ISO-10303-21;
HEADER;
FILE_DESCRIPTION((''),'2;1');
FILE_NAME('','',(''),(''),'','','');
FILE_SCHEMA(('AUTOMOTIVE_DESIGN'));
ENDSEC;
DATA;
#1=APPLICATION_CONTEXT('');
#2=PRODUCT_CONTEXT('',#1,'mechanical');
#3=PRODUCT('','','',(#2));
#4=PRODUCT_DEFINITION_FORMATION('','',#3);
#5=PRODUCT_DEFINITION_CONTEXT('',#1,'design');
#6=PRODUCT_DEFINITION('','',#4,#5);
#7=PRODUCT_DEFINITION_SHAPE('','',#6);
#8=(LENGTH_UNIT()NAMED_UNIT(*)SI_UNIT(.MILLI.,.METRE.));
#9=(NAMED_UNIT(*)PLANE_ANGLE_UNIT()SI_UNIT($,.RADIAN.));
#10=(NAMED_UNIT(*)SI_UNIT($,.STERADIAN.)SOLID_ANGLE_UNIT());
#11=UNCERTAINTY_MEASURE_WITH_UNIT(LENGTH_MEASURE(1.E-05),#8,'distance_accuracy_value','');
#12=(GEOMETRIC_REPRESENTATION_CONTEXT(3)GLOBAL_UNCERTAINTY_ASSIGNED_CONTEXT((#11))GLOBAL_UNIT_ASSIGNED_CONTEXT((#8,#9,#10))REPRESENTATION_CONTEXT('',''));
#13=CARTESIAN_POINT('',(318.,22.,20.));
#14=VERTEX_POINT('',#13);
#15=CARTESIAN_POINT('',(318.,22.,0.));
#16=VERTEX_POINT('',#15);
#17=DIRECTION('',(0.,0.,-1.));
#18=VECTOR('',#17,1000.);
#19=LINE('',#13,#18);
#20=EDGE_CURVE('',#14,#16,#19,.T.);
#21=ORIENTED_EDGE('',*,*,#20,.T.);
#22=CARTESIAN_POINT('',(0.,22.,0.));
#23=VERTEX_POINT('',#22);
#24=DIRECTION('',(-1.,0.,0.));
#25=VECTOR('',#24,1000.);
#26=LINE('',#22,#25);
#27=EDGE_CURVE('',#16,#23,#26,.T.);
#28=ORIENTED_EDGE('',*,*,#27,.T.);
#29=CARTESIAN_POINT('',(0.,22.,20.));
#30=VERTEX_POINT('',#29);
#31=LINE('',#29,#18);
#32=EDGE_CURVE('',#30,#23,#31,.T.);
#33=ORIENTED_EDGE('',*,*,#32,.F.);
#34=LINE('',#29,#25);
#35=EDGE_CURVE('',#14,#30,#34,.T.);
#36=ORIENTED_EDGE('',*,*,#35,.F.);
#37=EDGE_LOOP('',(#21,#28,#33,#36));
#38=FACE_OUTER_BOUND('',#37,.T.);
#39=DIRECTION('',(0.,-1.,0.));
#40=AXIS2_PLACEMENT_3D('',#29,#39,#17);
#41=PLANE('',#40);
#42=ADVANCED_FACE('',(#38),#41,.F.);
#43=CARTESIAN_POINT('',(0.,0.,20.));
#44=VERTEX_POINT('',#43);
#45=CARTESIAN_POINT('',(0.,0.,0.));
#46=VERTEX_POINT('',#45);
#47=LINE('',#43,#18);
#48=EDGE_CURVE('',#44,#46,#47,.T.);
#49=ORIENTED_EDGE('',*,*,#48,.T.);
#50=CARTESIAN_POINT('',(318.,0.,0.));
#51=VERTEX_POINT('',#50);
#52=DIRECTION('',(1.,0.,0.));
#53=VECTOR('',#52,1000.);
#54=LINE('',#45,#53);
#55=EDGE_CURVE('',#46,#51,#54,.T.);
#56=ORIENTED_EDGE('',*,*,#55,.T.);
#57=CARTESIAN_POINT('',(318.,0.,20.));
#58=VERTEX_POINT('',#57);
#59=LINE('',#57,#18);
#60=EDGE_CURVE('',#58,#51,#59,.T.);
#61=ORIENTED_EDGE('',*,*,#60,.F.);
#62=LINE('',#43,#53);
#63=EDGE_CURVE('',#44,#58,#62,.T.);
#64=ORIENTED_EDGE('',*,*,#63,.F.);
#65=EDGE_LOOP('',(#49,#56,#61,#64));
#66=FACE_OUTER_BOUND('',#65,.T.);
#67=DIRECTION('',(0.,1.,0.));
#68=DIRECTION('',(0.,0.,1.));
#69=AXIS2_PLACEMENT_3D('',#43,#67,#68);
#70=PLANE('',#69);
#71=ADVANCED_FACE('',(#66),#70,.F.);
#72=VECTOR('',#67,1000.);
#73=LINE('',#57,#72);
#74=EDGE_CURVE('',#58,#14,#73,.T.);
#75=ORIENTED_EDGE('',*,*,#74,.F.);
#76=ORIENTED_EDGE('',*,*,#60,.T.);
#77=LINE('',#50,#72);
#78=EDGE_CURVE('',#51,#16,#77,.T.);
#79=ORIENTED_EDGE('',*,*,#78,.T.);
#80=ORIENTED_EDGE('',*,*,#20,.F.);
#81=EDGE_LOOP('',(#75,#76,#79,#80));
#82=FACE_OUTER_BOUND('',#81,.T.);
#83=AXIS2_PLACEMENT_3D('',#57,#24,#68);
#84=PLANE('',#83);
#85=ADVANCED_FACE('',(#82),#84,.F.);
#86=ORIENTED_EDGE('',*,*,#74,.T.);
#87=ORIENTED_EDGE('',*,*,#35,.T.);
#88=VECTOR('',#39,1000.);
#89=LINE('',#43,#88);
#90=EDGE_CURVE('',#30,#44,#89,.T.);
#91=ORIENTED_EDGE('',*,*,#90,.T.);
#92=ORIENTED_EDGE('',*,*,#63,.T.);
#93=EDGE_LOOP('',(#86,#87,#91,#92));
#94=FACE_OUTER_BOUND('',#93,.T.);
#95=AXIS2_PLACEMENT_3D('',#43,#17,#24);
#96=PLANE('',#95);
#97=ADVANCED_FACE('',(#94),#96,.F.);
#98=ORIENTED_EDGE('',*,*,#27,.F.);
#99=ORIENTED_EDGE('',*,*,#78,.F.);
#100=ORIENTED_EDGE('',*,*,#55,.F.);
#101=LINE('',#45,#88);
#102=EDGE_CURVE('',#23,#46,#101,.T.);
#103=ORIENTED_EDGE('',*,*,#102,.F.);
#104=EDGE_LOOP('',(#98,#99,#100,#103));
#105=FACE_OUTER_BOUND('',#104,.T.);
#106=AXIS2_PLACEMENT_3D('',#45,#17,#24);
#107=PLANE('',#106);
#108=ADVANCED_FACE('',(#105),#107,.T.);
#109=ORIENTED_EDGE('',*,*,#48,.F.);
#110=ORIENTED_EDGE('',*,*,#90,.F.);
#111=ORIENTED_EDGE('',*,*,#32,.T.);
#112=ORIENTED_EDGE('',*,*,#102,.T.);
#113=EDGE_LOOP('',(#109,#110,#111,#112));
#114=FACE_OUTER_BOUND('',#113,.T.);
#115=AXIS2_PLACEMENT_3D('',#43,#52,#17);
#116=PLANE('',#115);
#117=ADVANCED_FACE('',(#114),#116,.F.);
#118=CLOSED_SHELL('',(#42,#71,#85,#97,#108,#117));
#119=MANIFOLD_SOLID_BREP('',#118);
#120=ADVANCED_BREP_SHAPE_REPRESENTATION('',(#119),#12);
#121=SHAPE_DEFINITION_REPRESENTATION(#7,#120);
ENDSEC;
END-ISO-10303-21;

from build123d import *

# Parameters (mm, degrees)
SKETCH1_W           = 318
SKETCH1_H           = 22
BOSS_EXTRUDE1_DEPTH = 20


with BuildPart() as part:
    # Sketch1 → Boss-Extrude1 (new body)
    with BuildSketch(Plane.XY):
        with Locations((159, 11)):
            Rectangle(SKETCH1_W, SKETCH1_H)
    extrude(amount=BOSS_EXTRUDE1_DEPTH)


solid = part.part
